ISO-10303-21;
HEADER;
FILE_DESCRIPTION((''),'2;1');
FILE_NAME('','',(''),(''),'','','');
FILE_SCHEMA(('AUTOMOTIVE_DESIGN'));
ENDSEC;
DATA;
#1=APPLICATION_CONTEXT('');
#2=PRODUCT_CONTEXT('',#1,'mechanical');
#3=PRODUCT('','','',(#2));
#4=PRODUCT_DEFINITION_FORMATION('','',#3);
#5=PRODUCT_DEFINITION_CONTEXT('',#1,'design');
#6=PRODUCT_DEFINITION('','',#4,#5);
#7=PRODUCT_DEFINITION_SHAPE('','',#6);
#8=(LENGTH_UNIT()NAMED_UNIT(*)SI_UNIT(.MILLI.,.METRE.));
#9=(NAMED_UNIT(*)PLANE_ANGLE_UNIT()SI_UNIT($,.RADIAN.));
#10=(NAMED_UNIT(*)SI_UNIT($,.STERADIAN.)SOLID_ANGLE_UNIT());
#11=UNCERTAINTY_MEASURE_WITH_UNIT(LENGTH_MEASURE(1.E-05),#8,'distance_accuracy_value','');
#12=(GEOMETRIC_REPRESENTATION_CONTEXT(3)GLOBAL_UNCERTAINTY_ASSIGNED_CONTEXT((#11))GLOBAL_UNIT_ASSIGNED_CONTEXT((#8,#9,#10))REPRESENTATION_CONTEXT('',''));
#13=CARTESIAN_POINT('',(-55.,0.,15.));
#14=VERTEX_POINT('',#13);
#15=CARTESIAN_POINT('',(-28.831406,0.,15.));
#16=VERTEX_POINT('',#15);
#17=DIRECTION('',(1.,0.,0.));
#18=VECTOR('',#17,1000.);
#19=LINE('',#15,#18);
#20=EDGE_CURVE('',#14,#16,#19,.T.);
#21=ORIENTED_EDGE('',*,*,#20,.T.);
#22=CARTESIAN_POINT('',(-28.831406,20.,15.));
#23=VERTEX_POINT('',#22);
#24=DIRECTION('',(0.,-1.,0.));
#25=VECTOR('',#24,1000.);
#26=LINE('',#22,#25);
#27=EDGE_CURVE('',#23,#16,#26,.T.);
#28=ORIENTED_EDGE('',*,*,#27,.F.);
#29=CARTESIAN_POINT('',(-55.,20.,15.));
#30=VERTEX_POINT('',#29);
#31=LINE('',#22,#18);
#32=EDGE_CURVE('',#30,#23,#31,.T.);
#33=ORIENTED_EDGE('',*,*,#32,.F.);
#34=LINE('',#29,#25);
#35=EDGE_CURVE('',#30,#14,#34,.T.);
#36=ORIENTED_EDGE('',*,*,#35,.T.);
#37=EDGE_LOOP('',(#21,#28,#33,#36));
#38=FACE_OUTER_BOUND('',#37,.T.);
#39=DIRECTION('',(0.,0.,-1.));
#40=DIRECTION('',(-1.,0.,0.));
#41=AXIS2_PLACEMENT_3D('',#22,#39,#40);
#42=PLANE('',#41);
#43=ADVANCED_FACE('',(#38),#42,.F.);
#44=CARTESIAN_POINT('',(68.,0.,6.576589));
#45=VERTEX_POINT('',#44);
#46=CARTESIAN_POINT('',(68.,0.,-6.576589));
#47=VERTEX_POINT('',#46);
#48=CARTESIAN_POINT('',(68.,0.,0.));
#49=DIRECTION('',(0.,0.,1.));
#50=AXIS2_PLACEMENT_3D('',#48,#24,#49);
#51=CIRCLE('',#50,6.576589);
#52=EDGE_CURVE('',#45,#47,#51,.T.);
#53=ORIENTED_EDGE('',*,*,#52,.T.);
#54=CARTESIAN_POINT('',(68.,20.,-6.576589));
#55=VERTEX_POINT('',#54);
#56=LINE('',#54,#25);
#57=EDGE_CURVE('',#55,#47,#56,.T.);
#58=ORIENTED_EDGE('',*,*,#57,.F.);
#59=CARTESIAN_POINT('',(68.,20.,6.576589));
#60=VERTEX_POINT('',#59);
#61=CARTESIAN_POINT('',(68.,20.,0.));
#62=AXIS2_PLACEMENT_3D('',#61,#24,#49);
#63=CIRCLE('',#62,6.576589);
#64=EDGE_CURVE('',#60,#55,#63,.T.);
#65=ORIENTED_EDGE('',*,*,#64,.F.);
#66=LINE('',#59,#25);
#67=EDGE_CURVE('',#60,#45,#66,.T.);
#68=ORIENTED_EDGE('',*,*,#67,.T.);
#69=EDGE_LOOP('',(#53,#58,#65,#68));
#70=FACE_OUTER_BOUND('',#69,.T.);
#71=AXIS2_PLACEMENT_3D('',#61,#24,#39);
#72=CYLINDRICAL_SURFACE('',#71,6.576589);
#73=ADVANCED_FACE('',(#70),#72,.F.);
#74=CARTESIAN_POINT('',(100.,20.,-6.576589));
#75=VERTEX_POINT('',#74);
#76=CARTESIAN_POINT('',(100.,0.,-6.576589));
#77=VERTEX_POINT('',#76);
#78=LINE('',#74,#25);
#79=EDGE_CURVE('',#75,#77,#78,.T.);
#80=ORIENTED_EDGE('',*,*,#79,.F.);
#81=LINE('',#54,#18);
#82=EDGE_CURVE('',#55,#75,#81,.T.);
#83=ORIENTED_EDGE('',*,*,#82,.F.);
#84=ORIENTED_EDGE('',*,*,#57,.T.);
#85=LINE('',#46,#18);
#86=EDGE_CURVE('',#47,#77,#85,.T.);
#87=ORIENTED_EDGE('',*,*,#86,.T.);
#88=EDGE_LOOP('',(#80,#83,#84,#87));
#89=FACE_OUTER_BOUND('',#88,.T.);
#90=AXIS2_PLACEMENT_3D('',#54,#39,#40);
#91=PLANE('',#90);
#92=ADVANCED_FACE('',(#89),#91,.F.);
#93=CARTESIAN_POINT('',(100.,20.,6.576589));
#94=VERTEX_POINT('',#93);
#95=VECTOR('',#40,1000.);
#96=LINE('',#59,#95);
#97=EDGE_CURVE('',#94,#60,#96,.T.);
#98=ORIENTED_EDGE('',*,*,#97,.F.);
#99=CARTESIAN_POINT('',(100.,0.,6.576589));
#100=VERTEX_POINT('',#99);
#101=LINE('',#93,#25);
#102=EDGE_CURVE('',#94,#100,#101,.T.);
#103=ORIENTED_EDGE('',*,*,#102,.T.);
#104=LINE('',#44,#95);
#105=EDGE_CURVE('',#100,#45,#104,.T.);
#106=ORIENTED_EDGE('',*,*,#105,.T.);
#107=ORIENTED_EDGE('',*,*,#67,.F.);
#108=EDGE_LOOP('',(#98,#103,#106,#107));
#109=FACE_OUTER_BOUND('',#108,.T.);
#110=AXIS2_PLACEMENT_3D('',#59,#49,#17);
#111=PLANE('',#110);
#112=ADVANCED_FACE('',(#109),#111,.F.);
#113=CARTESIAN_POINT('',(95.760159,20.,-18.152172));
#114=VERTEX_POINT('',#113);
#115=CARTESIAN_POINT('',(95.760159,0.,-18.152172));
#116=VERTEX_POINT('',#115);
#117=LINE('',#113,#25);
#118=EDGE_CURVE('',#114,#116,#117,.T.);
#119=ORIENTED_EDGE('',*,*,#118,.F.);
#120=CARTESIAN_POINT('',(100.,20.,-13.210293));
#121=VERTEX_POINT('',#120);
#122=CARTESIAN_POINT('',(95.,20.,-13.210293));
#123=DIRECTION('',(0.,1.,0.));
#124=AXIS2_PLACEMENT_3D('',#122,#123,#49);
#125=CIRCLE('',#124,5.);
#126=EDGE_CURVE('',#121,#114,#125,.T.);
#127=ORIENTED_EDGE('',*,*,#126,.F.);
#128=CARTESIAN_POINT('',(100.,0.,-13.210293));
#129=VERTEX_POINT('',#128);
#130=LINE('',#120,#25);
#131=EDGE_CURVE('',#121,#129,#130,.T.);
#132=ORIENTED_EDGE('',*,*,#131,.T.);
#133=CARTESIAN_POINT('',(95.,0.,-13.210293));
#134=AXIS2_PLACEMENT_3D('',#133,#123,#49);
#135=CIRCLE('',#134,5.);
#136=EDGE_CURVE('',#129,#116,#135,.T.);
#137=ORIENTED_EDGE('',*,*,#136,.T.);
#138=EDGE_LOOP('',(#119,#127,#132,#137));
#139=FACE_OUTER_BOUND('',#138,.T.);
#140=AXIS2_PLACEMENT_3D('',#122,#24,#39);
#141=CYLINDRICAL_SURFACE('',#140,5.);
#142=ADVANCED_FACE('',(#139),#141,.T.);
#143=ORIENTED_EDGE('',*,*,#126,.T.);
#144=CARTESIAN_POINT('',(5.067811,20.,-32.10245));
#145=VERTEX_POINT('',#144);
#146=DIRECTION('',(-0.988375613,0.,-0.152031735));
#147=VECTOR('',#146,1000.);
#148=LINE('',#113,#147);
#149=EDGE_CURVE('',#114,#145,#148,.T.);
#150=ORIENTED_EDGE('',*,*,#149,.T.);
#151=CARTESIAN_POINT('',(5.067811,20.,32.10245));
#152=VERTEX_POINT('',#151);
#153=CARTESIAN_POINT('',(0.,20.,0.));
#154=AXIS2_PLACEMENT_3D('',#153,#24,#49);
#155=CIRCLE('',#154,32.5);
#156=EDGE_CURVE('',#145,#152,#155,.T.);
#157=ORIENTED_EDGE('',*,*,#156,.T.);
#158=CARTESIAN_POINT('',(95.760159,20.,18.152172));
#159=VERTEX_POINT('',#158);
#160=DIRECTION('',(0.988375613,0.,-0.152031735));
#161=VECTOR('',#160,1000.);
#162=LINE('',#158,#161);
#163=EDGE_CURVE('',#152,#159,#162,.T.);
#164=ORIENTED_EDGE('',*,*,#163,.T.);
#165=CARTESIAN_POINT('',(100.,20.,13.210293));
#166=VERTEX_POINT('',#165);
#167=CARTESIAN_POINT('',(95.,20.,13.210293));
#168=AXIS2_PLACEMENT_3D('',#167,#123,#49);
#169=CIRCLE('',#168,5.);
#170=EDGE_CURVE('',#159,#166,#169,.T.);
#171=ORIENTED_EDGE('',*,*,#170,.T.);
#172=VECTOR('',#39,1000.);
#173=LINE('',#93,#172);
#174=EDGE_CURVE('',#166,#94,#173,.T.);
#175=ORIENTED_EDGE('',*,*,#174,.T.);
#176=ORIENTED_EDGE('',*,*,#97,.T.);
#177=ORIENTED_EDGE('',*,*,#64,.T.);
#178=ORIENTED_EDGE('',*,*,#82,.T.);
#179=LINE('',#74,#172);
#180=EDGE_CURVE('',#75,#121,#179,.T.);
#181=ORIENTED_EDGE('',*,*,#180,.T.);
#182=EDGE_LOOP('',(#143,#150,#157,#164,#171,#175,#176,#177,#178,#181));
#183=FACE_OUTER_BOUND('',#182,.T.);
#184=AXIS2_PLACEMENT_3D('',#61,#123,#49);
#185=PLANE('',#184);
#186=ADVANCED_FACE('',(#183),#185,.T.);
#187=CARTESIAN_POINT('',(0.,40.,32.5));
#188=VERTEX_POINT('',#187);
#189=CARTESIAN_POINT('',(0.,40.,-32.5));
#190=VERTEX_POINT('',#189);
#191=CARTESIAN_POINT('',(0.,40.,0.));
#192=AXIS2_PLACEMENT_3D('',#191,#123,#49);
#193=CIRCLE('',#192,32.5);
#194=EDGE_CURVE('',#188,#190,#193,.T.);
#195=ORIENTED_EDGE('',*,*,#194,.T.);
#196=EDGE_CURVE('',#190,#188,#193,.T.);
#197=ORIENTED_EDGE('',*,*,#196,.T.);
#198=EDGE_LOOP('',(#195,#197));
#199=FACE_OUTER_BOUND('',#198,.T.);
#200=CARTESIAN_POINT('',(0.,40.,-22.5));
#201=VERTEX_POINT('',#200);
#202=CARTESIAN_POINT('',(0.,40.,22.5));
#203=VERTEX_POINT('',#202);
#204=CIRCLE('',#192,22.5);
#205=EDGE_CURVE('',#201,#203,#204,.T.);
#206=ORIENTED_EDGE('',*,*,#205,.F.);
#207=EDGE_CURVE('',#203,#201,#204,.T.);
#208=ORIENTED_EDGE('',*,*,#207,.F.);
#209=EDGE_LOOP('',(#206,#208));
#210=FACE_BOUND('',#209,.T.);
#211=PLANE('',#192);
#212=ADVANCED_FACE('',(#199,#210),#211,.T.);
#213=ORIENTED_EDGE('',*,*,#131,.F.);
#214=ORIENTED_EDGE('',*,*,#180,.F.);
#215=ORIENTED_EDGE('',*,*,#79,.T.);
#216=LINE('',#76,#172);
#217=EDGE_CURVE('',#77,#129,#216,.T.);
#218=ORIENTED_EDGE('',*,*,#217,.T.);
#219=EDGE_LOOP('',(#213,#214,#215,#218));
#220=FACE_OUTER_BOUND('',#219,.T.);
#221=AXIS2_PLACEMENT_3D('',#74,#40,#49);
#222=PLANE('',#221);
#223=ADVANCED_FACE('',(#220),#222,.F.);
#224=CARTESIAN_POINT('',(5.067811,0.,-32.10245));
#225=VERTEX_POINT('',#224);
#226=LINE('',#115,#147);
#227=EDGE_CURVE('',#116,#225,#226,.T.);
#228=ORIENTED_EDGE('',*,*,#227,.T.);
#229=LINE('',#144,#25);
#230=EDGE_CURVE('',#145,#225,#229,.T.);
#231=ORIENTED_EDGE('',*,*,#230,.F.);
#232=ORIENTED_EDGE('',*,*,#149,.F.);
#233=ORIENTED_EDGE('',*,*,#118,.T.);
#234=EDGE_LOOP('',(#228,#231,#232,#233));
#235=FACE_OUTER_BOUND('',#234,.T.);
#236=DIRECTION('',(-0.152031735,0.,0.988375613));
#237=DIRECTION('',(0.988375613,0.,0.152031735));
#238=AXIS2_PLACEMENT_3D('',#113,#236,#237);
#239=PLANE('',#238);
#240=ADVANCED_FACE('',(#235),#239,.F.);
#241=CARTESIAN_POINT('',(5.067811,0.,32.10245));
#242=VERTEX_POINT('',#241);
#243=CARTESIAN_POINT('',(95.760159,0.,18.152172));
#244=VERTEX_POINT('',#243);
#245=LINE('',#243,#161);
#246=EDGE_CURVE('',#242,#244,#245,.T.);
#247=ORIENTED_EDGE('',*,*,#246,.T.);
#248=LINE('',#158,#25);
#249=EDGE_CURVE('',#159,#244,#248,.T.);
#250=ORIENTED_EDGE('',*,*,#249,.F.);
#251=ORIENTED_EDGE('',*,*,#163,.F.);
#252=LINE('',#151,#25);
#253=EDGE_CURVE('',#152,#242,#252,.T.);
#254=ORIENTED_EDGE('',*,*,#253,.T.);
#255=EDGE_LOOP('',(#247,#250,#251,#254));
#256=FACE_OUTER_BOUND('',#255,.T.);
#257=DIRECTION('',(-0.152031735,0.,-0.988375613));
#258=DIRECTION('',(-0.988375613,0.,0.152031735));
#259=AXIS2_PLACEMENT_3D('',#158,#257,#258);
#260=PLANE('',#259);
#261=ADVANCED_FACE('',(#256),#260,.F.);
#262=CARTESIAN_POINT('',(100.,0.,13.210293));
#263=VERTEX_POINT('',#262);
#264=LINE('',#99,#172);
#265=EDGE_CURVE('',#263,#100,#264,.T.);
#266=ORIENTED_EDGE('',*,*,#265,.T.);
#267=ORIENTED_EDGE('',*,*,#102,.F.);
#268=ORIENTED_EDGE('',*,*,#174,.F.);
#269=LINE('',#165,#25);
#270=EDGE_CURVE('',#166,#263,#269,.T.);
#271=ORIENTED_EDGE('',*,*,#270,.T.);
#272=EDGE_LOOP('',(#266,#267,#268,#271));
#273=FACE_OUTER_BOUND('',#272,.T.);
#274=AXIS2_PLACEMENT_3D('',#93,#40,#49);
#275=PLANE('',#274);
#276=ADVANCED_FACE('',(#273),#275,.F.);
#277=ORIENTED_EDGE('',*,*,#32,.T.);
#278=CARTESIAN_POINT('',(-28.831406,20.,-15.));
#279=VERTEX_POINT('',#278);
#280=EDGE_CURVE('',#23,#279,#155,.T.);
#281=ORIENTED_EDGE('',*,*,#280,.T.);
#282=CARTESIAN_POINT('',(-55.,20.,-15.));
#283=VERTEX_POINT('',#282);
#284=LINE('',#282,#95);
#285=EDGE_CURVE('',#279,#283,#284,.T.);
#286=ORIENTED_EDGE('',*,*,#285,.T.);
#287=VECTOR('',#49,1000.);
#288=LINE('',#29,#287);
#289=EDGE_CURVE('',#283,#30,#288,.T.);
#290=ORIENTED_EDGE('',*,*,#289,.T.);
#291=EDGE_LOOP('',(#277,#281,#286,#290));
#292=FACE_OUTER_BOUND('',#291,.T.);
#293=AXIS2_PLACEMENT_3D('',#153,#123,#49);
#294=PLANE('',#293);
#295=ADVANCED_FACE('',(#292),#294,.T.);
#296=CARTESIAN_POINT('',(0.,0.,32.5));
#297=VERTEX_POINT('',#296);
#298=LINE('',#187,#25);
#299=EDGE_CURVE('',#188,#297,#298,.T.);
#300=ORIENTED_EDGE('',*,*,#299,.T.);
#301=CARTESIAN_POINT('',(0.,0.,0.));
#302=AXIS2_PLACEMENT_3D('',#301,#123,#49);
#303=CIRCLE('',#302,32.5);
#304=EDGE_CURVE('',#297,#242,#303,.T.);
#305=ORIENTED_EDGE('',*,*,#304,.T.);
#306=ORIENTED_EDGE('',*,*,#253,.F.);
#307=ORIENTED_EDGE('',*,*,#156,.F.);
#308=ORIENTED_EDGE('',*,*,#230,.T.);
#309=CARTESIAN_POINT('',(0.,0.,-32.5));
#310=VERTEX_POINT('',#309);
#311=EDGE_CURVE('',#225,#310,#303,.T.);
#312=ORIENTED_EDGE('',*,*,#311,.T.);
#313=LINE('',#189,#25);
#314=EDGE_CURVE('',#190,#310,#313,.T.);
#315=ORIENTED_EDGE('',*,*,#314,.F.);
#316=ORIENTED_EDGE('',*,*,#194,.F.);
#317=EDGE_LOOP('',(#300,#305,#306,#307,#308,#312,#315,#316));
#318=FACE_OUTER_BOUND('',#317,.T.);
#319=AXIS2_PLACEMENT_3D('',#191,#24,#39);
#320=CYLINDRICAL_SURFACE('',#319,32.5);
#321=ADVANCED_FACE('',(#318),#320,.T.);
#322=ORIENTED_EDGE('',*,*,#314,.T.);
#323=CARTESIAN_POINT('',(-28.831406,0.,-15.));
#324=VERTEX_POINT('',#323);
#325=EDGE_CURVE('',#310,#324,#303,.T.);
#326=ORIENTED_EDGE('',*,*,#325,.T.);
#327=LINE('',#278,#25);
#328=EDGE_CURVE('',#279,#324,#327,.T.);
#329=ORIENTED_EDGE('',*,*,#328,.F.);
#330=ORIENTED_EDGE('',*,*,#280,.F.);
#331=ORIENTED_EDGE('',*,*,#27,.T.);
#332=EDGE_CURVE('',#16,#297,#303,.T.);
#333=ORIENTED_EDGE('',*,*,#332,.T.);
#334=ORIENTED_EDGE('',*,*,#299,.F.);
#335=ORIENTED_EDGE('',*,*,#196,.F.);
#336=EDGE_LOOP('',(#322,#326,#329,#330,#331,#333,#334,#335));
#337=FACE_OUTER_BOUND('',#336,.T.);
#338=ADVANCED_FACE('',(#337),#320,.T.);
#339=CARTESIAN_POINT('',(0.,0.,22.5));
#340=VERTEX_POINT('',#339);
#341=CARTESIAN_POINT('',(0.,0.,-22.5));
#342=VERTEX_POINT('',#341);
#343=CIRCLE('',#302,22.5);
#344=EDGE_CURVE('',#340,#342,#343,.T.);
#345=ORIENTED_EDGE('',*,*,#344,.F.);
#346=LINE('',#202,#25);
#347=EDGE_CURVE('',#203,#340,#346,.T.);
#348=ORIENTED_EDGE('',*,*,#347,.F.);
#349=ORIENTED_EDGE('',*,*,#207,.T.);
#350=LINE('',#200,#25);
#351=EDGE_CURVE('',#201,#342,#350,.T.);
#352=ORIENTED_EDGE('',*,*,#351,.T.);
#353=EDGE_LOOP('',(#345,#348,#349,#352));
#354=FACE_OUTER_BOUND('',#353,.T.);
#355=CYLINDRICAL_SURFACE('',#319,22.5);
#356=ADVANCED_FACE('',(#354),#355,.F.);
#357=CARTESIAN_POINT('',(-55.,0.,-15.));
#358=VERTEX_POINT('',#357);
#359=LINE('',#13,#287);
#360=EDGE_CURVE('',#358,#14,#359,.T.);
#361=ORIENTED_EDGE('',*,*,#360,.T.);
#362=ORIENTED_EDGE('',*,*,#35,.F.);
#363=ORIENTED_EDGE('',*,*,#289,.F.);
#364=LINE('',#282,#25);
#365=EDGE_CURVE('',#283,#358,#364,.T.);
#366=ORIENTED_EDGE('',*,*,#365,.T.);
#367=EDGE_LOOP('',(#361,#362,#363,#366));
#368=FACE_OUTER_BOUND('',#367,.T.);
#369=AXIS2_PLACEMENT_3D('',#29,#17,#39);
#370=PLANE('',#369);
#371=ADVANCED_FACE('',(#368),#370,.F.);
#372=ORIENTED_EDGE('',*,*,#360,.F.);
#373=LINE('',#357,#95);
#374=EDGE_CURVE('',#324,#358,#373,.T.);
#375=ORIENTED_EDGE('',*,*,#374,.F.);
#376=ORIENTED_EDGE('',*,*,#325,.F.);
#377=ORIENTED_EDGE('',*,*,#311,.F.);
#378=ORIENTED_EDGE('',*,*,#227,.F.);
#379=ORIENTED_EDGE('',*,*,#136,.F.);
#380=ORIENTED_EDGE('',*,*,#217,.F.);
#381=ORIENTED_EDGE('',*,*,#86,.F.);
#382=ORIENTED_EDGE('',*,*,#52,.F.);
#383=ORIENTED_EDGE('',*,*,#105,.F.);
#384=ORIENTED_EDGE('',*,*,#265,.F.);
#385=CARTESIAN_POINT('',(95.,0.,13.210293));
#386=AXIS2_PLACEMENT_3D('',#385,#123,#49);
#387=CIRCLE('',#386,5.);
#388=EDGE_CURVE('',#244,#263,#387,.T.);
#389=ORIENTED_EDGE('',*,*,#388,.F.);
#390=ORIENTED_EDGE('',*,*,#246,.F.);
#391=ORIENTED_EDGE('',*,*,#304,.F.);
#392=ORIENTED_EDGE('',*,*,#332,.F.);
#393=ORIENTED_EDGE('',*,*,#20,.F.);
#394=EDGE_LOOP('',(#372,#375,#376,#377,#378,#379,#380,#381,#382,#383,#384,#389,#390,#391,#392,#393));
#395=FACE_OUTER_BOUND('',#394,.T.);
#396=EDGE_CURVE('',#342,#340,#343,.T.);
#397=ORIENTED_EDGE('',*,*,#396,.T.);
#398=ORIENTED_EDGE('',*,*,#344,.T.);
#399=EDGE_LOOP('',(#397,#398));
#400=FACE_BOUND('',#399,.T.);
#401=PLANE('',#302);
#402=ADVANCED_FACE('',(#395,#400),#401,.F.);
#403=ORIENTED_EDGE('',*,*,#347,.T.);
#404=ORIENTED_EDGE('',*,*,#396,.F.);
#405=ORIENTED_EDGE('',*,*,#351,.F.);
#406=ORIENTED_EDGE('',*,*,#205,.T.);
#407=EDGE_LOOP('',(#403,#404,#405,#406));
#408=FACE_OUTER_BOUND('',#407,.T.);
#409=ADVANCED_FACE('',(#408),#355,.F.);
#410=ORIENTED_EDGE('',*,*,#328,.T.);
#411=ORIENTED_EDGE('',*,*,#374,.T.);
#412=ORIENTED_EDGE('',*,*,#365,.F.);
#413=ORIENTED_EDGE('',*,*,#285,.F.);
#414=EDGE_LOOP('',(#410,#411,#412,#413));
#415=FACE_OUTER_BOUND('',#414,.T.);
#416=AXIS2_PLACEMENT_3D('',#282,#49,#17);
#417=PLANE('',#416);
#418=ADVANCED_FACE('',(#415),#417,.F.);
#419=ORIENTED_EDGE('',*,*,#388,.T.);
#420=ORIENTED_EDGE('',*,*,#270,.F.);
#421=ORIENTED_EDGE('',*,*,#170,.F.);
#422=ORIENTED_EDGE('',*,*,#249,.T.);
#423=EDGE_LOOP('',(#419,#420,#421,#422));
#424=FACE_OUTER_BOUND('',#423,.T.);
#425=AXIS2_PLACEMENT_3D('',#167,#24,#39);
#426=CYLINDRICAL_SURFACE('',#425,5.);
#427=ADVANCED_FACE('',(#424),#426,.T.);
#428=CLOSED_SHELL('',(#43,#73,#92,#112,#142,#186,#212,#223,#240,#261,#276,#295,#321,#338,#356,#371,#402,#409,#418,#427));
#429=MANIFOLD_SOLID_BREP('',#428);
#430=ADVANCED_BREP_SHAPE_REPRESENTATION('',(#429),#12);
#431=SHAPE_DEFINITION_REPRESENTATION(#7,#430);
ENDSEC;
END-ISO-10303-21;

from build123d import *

# Parameters (mm, degrees)
HUB_PROFILE_65_45_R   = 32.5
HUB_PROFILE_65_45_R_2 = 22.5
HUB_65_BORE_45_DEPTH  = 40
FORK_ARM_DEPTH        = 20
REAR_BLOCK_DEPTH      = 20


with BuildPart() as part:
    # Hub Profile Ø65-Ø45 → Hub Ø65 Bore Ø45 (new body)
    with BuildSketch(Plane(origin=(0, 0, 0), x_dir=(1, 0, 0), z_dir=(0, 1, 0))):
        with Locations(Location((0, 0, 0), (0, 0, 270))):
            Circle(HUB_PROFILE_65_45_R)
        with Locations(Location((0, 0, 0), (0, 0, 270))):
            Circle(HUB_PROFILE_65_45_R_2, mode=Mode.SUBTRACT)
    extrude(amount=HUB_65_BORE_45_DEPTH)

    # Fork Arm Profile → Fork Arm (add)
    with BuildSketch(Plane(origin=(0, 0, 0), x_dir=(1, 0, 0), z_dir=(0, 1, 0))):
        with BuildLine():
            Line((68, 6.576589216), (100, 6.576589216))
            Line((100, 6.576589216), (100, 13.210293464))
            ThreePointArc((100, 13.210293464), (98.79478546, 16.465996662), (95.760158675, 18.152171527))
            Line((95.760158675, 18.152171527), (5.067811416, 32.102449867))
            ThreePointArc((5.067811416, 32.102449867), (32.5, 0), (5.067811416, -32.102449867))
            Line((5.067811416, -32.102449867), (95.760158675, -18.152171527))
            ThreePointArc((95.760158675, -18.152171527), (98.79478546, -16.465996662), (100, -13.210293464))
            Line((100, -13.210293464), (100, -6.576589216))
            Line((100, -6.576589216), (68, -6.576589216))
            ThreePointArc((68, -6.576589216), (61.423410784, 0), (68, 6.576589216))
        make_face()
    extrude(amount=FORK_ARM_DEPTH)

    # Rear Block Profile 30x55 → Rear Block (add)
    with BuildSketch(Plane(origin=(0, 0, 0), x_dir=(1, 0, 0), z_dir=(0, 1, 0))):
        with BuildLine():
            Line((-55, -15), (-55, 15))
            Line((-55, 15), (-28.831406487, 15))
            ThreePointArc((-28.831406487, 15), (-32.5, 0), (-28.831406487, -15))
            Line((-28.831406487, -15), (-55, -15))
        make_face()
    extrude(amount=REAR_BLOCK_DEPTH)


solid = part.part
